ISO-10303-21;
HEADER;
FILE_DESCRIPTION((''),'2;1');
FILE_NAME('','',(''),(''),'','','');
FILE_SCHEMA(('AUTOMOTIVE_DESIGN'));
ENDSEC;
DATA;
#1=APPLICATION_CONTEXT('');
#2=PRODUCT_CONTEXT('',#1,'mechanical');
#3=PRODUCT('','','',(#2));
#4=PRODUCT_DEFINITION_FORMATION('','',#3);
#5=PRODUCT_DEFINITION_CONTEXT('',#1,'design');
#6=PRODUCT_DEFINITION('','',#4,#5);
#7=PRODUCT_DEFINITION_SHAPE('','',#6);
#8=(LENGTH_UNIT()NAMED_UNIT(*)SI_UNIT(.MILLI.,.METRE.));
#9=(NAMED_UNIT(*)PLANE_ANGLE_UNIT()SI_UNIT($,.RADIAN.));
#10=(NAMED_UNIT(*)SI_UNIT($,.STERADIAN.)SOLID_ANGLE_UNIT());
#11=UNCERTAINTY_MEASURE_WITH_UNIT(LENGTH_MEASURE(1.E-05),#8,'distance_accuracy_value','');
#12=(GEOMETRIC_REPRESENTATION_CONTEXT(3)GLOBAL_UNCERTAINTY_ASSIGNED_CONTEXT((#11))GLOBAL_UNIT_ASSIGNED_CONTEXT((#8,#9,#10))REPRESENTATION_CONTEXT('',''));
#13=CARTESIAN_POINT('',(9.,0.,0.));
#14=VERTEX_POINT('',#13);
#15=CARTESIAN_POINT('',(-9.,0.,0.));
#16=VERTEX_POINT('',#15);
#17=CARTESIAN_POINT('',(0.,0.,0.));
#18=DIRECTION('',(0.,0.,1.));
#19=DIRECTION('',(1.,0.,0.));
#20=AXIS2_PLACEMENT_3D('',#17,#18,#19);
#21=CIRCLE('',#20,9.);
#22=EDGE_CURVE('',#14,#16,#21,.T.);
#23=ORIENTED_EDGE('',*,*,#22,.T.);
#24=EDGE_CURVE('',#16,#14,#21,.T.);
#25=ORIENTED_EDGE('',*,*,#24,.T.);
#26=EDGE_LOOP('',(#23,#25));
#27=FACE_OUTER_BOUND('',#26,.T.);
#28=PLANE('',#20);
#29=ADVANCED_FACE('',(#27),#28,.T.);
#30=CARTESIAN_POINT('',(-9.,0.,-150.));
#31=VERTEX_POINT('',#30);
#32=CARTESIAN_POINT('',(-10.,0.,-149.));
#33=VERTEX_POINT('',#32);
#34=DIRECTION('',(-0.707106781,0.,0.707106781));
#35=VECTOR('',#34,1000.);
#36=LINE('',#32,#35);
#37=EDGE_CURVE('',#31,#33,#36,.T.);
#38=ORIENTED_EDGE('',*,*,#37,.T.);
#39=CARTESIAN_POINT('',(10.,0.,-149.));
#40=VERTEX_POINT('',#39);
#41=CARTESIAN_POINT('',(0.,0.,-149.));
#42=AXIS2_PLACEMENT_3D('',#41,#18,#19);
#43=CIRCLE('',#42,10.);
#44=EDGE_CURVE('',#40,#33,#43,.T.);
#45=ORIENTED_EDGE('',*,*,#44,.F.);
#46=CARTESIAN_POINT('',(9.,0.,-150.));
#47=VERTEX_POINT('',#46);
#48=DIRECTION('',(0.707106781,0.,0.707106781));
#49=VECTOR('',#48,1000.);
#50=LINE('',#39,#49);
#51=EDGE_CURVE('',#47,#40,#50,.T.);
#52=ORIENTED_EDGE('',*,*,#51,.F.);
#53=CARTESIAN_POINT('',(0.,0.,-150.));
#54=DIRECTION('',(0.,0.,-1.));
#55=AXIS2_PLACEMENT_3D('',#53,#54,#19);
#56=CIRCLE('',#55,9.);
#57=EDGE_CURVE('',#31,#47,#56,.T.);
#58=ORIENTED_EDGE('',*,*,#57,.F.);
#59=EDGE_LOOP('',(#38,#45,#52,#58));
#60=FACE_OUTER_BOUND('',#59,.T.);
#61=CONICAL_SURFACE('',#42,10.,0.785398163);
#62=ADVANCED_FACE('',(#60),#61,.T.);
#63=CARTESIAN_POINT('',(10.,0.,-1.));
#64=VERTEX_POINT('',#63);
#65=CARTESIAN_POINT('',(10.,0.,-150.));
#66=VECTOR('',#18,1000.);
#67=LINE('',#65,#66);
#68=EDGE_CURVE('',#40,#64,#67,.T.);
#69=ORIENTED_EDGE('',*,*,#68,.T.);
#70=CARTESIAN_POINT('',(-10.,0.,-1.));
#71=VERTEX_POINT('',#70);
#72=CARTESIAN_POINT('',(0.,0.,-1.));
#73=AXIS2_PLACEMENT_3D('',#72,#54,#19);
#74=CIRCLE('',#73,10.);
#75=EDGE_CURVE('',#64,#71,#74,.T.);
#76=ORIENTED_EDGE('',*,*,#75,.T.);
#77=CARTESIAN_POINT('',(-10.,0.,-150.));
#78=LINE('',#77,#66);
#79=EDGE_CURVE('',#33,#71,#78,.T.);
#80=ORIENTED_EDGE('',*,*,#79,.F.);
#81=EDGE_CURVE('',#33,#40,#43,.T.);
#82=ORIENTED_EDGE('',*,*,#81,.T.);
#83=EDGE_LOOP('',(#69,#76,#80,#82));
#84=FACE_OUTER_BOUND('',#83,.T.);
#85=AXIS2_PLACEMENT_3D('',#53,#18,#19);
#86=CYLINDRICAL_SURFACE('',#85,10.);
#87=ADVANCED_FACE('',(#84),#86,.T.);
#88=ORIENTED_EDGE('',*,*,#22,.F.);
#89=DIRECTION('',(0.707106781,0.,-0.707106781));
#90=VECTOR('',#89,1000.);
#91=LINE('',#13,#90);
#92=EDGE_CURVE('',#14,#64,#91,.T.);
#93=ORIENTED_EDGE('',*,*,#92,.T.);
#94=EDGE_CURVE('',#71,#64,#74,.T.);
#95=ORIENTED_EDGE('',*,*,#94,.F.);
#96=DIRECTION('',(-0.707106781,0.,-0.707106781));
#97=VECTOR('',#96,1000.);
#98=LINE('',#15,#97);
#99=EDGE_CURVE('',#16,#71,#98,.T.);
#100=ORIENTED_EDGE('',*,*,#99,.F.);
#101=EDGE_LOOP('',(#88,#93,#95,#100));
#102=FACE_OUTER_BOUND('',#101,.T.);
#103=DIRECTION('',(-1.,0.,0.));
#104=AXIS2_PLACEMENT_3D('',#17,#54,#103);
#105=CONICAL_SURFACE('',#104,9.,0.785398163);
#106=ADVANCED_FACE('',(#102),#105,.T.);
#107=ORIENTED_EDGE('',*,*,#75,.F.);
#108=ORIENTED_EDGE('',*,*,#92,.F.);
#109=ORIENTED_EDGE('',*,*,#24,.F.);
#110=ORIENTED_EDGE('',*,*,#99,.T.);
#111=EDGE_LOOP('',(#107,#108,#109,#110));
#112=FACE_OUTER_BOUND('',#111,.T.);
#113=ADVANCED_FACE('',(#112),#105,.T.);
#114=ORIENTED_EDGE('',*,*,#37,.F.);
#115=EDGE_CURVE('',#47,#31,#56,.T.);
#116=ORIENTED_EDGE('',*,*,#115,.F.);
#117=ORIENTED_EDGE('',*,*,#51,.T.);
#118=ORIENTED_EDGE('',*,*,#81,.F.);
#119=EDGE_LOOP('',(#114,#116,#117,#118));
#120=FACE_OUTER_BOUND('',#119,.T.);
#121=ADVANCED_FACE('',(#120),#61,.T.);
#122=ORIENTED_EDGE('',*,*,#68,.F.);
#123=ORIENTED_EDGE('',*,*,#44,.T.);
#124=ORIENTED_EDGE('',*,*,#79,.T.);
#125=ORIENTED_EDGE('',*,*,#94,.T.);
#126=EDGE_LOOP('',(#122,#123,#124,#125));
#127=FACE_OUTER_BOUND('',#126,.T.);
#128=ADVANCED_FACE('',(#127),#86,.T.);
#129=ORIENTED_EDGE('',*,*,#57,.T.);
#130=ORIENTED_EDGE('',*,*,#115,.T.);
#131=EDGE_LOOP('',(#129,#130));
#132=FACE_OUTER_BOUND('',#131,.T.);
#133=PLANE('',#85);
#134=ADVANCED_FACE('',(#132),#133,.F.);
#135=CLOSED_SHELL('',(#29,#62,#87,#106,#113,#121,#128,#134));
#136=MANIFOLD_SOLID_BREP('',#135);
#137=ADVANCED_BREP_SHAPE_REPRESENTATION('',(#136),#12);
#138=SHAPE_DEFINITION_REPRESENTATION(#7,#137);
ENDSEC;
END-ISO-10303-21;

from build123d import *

# Parameters (mm, degrees)
SKETCH1_R           = 10
BOSS_EXTRUDE1_DEPTH = 150
CHAMFER1_SIZE       = 1


with BuildPart() as part:
    # Sketch1 → Boss-Extrude1 (new body)
    with BuildSketch(Plane.XY):
        Circle(SKETCH1_R)
    extrude(amount=-BOSS_EXTRUDE1_DEPTH)

    # Chamfer1
    chamfer1_edges = [part.edges().sort_by_distance(p)[0] for p in [
        (-10, 0, 0),
        (-10, 0, -150),
    ]]
    chamfer(chamfer1_edges, length=CHAMFER1_SIZE)


solid = part.part
